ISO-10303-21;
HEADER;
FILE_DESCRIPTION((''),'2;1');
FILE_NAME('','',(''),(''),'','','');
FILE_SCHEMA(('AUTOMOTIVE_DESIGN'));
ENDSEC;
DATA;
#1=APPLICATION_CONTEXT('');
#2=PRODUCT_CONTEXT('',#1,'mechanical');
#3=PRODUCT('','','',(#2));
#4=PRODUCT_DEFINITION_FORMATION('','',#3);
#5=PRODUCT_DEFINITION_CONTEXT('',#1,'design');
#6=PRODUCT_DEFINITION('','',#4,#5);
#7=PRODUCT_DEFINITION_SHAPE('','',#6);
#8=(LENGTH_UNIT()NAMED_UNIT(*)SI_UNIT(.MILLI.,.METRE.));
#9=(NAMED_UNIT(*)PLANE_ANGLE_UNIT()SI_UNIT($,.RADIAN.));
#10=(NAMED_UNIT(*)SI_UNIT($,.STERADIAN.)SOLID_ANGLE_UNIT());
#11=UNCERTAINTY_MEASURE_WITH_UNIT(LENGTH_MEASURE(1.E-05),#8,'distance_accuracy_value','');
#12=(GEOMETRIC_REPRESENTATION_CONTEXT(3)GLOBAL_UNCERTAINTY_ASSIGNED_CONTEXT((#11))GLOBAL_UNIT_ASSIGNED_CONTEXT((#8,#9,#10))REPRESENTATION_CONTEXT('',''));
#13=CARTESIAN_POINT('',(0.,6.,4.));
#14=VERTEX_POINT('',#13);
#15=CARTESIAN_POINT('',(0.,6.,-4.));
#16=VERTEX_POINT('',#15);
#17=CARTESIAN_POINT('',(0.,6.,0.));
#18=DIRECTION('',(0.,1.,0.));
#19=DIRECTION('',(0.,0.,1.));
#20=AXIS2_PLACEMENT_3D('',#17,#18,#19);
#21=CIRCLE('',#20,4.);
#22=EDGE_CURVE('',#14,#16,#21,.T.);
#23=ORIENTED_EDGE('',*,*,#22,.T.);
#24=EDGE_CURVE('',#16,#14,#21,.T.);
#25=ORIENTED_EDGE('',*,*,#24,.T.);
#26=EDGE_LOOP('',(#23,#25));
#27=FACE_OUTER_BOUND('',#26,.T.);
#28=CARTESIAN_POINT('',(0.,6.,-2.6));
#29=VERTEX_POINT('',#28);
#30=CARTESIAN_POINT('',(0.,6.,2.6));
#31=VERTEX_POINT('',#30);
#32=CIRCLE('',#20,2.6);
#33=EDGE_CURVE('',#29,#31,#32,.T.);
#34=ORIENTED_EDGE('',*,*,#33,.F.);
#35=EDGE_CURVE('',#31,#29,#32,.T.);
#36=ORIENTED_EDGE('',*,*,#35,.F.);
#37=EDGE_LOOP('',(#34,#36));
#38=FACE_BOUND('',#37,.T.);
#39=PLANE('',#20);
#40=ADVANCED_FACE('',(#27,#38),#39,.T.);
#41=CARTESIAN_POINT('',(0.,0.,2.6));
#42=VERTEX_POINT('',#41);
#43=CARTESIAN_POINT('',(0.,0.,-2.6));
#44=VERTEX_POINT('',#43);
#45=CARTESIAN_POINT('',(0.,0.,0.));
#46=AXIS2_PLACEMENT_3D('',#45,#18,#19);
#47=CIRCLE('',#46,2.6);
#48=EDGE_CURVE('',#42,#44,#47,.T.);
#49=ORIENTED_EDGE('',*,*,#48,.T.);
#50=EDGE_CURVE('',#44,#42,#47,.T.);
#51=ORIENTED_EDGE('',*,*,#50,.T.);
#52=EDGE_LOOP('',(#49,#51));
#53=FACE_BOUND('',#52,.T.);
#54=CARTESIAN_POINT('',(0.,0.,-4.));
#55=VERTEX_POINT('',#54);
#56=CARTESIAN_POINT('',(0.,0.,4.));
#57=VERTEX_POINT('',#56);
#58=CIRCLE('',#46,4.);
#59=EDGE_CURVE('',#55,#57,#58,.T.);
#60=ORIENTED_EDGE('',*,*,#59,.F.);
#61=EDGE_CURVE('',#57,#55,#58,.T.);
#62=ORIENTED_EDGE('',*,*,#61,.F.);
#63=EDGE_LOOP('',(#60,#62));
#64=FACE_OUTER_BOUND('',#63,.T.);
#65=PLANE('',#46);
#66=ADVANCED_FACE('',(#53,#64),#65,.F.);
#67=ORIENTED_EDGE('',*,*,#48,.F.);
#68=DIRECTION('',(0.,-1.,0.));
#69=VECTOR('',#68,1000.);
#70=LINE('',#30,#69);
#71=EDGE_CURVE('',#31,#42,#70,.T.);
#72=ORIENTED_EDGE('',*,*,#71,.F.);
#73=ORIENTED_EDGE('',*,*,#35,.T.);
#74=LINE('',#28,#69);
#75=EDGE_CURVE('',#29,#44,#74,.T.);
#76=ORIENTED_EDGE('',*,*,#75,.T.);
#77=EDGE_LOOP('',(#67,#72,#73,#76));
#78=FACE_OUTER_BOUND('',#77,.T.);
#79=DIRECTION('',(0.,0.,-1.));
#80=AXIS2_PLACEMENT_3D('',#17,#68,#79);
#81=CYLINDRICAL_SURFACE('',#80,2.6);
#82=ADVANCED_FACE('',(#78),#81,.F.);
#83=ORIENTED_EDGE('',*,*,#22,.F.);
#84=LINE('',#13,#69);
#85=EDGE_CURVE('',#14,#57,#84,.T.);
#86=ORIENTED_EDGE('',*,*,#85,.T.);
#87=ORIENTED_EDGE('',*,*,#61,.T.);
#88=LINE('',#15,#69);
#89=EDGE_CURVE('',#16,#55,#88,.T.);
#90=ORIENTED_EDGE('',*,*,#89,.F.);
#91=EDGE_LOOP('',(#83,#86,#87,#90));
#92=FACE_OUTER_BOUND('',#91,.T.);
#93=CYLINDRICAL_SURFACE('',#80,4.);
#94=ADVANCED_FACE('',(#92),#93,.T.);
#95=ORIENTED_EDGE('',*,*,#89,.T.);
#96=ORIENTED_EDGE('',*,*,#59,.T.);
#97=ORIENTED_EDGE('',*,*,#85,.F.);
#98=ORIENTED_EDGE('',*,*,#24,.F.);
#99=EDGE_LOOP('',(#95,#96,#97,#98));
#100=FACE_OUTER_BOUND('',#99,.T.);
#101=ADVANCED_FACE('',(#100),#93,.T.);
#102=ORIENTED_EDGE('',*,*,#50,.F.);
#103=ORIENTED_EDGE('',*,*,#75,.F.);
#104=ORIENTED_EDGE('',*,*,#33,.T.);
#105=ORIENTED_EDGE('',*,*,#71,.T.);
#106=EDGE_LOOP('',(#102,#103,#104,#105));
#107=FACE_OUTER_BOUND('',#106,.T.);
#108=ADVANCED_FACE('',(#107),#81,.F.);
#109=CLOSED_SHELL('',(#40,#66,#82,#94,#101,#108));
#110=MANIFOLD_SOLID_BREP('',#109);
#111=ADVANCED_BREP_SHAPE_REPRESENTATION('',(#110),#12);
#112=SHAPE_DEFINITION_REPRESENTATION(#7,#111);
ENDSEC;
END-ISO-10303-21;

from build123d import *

# Parameters (mm, degrees)
SKETCH1_R           = 4
SKETCH1_R_2         = 2.6
BOSS_EXTRUDE1_DEPTH = 6


with BuildPart() as part:
    # Sketch1 → Boss-Extrude1 (new body)
    with BuildSketch(Plane(origin=(0, 0, 0), x_dir=(1, 0, 0), z_dir=(0, 1, 0))):
        with Locations(Location((0, 0, 0), (0, 0, 270))):
            Circle(SKETCH1_R)
        with Locations(Location((0, 0, 0), (0, 0, 270))):
            Circle(SKETCH1_R_2, mode=Mode.SUBTRACT)
    extrude(amount=BOSS_EXTRUDE1_DEPTH)


solid = part.part
